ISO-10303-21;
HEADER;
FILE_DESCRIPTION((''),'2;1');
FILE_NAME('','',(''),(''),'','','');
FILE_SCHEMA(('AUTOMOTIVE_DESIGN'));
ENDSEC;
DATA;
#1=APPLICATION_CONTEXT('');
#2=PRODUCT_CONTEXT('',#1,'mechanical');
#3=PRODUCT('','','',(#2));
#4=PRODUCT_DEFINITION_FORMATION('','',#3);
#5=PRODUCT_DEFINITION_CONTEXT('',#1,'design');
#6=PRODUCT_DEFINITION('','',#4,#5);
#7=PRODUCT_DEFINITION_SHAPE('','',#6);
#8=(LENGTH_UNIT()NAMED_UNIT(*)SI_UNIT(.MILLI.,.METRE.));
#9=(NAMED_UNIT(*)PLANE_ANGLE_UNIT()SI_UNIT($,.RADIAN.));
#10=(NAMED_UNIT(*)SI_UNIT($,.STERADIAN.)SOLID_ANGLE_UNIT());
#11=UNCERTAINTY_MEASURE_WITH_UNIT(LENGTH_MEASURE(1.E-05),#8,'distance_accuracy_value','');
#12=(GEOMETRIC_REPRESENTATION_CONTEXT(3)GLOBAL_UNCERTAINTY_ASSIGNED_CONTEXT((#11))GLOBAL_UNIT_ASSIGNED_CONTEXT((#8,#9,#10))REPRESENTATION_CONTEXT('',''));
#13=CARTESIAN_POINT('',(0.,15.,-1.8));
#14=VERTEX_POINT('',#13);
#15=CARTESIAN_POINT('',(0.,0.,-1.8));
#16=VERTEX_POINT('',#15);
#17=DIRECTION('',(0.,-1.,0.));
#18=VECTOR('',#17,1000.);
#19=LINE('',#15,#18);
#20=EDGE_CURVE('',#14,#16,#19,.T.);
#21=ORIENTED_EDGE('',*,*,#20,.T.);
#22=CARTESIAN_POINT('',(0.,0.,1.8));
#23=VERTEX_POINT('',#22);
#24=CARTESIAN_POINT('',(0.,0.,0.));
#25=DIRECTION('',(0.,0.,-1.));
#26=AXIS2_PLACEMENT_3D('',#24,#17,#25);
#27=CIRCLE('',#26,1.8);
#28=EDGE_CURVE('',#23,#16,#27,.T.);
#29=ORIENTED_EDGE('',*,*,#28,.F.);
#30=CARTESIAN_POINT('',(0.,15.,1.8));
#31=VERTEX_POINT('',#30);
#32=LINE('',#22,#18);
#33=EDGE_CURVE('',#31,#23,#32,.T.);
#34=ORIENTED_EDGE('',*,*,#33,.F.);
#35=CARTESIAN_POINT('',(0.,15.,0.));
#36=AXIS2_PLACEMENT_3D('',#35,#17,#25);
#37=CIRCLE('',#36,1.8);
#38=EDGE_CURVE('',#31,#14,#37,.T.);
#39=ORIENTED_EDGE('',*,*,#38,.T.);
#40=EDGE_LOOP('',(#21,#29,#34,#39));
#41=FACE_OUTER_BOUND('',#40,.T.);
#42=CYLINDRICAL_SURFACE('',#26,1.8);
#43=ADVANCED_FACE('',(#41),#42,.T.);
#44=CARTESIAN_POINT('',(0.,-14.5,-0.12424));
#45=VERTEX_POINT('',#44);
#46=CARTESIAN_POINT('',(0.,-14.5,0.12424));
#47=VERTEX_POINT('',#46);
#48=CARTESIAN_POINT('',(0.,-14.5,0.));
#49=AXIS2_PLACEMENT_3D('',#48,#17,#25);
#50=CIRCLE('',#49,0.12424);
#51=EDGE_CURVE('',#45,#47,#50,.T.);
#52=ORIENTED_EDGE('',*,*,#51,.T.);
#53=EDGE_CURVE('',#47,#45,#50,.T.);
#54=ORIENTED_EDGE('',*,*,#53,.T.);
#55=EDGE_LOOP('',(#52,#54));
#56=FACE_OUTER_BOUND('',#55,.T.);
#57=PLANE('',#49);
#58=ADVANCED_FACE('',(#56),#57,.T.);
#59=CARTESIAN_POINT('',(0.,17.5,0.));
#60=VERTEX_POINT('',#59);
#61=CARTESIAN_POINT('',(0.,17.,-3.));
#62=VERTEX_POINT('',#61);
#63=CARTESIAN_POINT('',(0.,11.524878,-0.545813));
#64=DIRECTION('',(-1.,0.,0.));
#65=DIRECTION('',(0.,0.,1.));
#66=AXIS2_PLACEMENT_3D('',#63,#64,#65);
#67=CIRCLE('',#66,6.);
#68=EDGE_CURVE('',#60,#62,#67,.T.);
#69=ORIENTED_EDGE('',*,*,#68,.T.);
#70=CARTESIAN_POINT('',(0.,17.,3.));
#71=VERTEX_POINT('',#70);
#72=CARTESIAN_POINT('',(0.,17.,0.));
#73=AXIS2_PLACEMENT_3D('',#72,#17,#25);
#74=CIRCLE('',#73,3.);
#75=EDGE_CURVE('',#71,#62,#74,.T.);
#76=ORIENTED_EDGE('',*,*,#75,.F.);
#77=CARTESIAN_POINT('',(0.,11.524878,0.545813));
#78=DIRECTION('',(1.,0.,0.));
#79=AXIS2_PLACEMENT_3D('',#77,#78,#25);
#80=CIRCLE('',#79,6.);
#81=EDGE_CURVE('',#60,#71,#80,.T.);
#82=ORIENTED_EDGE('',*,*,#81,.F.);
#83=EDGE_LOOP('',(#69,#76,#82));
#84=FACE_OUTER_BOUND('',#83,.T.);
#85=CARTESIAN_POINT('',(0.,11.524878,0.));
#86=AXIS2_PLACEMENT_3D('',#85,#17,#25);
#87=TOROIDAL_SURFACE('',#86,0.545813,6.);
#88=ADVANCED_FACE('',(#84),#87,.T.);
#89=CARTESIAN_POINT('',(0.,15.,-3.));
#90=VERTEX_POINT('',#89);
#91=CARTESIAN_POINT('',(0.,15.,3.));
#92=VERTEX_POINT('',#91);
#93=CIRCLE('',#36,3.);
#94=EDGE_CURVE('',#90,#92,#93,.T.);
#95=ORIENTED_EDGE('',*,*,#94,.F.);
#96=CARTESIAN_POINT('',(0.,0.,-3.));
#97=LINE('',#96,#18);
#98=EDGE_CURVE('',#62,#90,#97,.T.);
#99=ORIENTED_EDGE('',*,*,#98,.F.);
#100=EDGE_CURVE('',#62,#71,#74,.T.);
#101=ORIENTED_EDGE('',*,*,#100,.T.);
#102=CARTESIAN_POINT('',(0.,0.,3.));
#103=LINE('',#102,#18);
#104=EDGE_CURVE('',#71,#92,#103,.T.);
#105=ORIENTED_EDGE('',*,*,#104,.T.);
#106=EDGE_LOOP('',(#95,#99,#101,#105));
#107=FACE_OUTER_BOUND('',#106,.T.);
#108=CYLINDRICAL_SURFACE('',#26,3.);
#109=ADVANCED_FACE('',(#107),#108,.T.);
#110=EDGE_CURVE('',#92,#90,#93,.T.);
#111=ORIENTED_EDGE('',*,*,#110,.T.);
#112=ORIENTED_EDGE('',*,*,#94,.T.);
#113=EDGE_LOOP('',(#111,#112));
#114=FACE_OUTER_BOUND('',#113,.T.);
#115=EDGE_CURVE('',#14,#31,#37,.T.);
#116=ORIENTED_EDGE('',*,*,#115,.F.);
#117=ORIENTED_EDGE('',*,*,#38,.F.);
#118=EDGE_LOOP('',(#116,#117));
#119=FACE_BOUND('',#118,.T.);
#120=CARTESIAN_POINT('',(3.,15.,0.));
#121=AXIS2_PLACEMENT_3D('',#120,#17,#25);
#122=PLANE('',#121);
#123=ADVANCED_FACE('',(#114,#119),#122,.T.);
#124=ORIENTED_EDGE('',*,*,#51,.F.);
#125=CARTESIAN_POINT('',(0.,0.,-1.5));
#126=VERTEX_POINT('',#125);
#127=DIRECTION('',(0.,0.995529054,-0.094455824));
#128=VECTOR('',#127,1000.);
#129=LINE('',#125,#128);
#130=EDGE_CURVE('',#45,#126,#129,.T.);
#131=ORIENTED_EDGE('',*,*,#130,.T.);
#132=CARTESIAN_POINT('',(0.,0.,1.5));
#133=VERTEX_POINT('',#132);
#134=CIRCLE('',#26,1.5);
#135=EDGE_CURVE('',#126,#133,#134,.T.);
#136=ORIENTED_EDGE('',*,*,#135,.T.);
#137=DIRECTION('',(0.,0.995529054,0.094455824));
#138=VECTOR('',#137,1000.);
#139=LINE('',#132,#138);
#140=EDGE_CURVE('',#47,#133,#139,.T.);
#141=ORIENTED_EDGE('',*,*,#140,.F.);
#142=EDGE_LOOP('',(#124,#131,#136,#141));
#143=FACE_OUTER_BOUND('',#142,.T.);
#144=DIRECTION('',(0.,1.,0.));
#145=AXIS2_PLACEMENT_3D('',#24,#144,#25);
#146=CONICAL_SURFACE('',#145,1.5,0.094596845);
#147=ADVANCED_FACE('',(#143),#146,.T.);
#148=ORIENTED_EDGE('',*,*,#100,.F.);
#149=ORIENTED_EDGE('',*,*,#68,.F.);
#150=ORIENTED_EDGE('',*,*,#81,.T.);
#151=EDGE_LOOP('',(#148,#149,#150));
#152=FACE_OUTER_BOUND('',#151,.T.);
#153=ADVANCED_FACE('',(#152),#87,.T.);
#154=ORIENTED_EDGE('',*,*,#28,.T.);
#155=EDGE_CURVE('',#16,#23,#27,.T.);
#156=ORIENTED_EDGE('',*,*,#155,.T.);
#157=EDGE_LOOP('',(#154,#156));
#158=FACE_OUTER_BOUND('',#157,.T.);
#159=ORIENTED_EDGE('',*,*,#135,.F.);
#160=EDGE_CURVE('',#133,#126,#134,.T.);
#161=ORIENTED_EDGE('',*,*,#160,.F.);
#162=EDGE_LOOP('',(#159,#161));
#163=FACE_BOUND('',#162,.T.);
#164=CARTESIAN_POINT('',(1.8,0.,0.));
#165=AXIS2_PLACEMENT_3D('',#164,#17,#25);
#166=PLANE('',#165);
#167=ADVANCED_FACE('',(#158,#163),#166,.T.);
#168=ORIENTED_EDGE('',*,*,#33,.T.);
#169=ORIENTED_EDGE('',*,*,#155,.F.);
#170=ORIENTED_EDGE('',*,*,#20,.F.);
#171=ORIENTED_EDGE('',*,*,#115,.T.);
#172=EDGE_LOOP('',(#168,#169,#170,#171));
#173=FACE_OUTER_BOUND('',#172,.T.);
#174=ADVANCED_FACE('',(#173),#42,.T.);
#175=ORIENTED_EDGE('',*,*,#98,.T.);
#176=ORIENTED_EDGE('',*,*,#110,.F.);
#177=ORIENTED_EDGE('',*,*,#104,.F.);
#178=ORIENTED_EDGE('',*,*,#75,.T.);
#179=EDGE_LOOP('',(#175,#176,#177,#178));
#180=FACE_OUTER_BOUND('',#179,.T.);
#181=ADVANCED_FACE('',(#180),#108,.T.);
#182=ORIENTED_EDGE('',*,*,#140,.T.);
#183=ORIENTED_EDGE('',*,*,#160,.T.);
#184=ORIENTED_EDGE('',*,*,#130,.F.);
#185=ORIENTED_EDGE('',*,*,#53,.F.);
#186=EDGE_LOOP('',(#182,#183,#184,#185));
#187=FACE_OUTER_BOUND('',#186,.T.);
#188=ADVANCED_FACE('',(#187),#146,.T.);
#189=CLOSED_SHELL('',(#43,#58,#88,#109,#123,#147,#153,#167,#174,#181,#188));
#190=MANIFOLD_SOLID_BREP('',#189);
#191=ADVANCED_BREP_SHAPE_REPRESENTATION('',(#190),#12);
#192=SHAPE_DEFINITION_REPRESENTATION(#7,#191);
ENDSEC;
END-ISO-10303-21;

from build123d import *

# Parameters (mm, degrees)
TIP_BASE_CIRCLE_3_R      = 1.5
TAPERED_NEEDLE_TIP_DEPTH = 14.5
TAPERED_NEEDLE_TIP_TAPER = 5.42


with BuildPart() as part:
    # Head and Stem Profile → Head and Stem Revolve (revolve)
    with BuildSketch(Plane.XY, mode=Mode.PRIVATE) as head_and_stem_revolve_sk:
        with BuildLine():
            Line((0, 0), (0, 17.5))
            ThreePointArc((0, 17.5), (1.532206849, 17.443241097), (3, 17))
            Line((3, 17), (3, 15))
            Line((3, 15), (1.8, 15))
            Line((1.8, 15), (1.8, 0))
            Line((1.8, 0), (0, 0))
        make_face()
    revolve(head_and_stem_revolve_sk.sketch.rotate(Axis((0, 0, 0), (0, 1, 0)), 90), axis=Axis((0, 0, 0), (0, 1, 0)))

    # Tip Base Circle Ø3 → Tapered Needle Tip (add)
    with BuildSketch(Plane.XZ):
        Circle(TIP_BASE_CIRCLE_3_R)
    extrude(amount=TAPERED_NEEDLE_TIP_DEPTH, taper=TAPERED_NEEDLE_TIP_TAPER)


solid = part.part
